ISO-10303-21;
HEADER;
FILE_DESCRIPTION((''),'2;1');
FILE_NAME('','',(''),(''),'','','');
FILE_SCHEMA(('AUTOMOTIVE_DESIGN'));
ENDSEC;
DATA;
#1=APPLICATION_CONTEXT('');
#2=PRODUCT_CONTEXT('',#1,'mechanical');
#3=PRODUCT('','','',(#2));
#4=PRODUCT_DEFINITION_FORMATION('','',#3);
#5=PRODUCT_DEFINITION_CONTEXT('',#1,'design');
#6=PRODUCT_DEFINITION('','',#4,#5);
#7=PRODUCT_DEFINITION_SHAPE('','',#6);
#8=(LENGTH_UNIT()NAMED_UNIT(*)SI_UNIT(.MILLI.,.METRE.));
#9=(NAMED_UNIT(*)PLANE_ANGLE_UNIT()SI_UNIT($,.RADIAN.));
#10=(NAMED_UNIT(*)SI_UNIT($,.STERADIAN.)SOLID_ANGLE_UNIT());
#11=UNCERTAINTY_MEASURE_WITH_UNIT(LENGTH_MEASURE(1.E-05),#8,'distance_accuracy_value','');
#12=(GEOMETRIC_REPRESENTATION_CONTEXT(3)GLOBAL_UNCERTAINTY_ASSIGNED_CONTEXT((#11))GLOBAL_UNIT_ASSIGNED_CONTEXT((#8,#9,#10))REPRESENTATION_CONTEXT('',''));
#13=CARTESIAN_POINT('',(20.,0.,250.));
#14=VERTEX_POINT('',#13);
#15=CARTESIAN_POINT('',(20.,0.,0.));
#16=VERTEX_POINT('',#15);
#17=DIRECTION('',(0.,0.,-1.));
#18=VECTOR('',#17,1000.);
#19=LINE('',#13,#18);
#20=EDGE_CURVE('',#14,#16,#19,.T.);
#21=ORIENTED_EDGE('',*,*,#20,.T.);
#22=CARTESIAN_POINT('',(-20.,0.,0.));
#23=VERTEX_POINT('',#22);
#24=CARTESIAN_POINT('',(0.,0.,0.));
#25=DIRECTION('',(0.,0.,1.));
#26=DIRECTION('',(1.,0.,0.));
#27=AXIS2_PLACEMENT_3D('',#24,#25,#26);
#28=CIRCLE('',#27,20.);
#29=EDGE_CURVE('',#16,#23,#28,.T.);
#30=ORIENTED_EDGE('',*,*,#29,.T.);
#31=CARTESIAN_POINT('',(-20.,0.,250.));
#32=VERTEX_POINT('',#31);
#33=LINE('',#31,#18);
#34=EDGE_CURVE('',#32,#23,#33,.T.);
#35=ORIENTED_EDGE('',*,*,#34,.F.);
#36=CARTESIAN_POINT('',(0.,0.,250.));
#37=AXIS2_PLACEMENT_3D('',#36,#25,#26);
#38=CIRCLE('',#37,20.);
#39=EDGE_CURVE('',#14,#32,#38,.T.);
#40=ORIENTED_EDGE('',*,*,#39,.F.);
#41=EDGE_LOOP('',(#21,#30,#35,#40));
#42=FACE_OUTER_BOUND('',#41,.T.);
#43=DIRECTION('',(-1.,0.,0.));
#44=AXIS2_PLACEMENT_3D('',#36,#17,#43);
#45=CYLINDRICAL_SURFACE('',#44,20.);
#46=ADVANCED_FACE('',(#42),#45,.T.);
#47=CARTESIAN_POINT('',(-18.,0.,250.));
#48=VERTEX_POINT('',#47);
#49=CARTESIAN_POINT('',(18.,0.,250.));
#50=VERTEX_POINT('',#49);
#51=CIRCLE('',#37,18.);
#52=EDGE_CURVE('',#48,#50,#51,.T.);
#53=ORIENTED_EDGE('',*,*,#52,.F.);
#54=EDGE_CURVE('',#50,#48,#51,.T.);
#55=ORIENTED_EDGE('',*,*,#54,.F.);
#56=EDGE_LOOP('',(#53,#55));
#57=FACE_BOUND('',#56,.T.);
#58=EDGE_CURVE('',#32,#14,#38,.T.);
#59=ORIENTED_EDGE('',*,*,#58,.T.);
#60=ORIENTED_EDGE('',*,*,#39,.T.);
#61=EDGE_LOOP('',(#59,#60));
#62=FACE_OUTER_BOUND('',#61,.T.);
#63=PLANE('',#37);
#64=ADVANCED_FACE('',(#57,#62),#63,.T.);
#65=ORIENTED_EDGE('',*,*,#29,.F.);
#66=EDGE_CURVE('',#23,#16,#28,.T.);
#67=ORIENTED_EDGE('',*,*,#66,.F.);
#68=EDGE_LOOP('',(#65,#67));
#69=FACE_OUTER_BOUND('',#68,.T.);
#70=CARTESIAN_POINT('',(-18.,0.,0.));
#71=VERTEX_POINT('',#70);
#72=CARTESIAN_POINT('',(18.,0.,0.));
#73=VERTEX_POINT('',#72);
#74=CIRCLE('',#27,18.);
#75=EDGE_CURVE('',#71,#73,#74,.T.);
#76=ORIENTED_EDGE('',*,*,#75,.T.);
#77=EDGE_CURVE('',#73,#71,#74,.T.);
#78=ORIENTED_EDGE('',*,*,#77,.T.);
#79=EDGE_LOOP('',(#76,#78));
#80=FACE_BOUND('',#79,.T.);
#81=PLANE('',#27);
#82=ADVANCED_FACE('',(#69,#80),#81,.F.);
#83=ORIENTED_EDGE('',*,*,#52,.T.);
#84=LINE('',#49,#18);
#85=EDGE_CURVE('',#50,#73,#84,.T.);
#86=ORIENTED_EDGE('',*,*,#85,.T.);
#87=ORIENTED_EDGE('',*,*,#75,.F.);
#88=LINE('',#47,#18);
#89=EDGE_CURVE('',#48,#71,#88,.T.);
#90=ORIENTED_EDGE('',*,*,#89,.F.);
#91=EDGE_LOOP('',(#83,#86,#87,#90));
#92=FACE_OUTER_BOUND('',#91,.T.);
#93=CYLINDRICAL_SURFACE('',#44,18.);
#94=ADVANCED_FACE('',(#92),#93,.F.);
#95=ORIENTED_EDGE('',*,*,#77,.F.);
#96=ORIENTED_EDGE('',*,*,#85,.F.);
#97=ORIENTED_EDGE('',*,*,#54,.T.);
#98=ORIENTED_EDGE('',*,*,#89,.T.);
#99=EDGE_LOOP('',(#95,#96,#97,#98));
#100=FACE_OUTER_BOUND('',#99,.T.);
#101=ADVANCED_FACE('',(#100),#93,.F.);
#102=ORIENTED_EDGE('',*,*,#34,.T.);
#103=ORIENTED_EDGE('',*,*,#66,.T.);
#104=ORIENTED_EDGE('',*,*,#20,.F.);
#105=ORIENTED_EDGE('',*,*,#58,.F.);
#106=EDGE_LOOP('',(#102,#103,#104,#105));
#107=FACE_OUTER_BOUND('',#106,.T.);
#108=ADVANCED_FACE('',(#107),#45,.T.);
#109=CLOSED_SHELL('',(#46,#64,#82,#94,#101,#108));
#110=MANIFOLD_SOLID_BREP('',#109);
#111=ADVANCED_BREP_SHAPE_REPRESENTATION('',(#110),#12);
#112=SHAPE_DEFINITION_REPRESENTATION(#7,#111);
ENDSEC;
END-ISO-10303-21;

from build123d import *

# Parameters (mm, degrees)
SKETCH_1_R      = 20
SKETCH_1_R_2    = 18
EXTRUDE_1_DEPTH = 250


with BuildPart() as part:
    # 草图1 → 凸台-拉伸1 (new body)
    with BuildSketch(Plane.XY):
        Circle(SKETCH_1_R)
        Circle(SKETCH_1_R_2, mode=Mode.SUBTRACT)
    extrude(amount=EXTRUDE_1_DEPTH)


solid = part.part
